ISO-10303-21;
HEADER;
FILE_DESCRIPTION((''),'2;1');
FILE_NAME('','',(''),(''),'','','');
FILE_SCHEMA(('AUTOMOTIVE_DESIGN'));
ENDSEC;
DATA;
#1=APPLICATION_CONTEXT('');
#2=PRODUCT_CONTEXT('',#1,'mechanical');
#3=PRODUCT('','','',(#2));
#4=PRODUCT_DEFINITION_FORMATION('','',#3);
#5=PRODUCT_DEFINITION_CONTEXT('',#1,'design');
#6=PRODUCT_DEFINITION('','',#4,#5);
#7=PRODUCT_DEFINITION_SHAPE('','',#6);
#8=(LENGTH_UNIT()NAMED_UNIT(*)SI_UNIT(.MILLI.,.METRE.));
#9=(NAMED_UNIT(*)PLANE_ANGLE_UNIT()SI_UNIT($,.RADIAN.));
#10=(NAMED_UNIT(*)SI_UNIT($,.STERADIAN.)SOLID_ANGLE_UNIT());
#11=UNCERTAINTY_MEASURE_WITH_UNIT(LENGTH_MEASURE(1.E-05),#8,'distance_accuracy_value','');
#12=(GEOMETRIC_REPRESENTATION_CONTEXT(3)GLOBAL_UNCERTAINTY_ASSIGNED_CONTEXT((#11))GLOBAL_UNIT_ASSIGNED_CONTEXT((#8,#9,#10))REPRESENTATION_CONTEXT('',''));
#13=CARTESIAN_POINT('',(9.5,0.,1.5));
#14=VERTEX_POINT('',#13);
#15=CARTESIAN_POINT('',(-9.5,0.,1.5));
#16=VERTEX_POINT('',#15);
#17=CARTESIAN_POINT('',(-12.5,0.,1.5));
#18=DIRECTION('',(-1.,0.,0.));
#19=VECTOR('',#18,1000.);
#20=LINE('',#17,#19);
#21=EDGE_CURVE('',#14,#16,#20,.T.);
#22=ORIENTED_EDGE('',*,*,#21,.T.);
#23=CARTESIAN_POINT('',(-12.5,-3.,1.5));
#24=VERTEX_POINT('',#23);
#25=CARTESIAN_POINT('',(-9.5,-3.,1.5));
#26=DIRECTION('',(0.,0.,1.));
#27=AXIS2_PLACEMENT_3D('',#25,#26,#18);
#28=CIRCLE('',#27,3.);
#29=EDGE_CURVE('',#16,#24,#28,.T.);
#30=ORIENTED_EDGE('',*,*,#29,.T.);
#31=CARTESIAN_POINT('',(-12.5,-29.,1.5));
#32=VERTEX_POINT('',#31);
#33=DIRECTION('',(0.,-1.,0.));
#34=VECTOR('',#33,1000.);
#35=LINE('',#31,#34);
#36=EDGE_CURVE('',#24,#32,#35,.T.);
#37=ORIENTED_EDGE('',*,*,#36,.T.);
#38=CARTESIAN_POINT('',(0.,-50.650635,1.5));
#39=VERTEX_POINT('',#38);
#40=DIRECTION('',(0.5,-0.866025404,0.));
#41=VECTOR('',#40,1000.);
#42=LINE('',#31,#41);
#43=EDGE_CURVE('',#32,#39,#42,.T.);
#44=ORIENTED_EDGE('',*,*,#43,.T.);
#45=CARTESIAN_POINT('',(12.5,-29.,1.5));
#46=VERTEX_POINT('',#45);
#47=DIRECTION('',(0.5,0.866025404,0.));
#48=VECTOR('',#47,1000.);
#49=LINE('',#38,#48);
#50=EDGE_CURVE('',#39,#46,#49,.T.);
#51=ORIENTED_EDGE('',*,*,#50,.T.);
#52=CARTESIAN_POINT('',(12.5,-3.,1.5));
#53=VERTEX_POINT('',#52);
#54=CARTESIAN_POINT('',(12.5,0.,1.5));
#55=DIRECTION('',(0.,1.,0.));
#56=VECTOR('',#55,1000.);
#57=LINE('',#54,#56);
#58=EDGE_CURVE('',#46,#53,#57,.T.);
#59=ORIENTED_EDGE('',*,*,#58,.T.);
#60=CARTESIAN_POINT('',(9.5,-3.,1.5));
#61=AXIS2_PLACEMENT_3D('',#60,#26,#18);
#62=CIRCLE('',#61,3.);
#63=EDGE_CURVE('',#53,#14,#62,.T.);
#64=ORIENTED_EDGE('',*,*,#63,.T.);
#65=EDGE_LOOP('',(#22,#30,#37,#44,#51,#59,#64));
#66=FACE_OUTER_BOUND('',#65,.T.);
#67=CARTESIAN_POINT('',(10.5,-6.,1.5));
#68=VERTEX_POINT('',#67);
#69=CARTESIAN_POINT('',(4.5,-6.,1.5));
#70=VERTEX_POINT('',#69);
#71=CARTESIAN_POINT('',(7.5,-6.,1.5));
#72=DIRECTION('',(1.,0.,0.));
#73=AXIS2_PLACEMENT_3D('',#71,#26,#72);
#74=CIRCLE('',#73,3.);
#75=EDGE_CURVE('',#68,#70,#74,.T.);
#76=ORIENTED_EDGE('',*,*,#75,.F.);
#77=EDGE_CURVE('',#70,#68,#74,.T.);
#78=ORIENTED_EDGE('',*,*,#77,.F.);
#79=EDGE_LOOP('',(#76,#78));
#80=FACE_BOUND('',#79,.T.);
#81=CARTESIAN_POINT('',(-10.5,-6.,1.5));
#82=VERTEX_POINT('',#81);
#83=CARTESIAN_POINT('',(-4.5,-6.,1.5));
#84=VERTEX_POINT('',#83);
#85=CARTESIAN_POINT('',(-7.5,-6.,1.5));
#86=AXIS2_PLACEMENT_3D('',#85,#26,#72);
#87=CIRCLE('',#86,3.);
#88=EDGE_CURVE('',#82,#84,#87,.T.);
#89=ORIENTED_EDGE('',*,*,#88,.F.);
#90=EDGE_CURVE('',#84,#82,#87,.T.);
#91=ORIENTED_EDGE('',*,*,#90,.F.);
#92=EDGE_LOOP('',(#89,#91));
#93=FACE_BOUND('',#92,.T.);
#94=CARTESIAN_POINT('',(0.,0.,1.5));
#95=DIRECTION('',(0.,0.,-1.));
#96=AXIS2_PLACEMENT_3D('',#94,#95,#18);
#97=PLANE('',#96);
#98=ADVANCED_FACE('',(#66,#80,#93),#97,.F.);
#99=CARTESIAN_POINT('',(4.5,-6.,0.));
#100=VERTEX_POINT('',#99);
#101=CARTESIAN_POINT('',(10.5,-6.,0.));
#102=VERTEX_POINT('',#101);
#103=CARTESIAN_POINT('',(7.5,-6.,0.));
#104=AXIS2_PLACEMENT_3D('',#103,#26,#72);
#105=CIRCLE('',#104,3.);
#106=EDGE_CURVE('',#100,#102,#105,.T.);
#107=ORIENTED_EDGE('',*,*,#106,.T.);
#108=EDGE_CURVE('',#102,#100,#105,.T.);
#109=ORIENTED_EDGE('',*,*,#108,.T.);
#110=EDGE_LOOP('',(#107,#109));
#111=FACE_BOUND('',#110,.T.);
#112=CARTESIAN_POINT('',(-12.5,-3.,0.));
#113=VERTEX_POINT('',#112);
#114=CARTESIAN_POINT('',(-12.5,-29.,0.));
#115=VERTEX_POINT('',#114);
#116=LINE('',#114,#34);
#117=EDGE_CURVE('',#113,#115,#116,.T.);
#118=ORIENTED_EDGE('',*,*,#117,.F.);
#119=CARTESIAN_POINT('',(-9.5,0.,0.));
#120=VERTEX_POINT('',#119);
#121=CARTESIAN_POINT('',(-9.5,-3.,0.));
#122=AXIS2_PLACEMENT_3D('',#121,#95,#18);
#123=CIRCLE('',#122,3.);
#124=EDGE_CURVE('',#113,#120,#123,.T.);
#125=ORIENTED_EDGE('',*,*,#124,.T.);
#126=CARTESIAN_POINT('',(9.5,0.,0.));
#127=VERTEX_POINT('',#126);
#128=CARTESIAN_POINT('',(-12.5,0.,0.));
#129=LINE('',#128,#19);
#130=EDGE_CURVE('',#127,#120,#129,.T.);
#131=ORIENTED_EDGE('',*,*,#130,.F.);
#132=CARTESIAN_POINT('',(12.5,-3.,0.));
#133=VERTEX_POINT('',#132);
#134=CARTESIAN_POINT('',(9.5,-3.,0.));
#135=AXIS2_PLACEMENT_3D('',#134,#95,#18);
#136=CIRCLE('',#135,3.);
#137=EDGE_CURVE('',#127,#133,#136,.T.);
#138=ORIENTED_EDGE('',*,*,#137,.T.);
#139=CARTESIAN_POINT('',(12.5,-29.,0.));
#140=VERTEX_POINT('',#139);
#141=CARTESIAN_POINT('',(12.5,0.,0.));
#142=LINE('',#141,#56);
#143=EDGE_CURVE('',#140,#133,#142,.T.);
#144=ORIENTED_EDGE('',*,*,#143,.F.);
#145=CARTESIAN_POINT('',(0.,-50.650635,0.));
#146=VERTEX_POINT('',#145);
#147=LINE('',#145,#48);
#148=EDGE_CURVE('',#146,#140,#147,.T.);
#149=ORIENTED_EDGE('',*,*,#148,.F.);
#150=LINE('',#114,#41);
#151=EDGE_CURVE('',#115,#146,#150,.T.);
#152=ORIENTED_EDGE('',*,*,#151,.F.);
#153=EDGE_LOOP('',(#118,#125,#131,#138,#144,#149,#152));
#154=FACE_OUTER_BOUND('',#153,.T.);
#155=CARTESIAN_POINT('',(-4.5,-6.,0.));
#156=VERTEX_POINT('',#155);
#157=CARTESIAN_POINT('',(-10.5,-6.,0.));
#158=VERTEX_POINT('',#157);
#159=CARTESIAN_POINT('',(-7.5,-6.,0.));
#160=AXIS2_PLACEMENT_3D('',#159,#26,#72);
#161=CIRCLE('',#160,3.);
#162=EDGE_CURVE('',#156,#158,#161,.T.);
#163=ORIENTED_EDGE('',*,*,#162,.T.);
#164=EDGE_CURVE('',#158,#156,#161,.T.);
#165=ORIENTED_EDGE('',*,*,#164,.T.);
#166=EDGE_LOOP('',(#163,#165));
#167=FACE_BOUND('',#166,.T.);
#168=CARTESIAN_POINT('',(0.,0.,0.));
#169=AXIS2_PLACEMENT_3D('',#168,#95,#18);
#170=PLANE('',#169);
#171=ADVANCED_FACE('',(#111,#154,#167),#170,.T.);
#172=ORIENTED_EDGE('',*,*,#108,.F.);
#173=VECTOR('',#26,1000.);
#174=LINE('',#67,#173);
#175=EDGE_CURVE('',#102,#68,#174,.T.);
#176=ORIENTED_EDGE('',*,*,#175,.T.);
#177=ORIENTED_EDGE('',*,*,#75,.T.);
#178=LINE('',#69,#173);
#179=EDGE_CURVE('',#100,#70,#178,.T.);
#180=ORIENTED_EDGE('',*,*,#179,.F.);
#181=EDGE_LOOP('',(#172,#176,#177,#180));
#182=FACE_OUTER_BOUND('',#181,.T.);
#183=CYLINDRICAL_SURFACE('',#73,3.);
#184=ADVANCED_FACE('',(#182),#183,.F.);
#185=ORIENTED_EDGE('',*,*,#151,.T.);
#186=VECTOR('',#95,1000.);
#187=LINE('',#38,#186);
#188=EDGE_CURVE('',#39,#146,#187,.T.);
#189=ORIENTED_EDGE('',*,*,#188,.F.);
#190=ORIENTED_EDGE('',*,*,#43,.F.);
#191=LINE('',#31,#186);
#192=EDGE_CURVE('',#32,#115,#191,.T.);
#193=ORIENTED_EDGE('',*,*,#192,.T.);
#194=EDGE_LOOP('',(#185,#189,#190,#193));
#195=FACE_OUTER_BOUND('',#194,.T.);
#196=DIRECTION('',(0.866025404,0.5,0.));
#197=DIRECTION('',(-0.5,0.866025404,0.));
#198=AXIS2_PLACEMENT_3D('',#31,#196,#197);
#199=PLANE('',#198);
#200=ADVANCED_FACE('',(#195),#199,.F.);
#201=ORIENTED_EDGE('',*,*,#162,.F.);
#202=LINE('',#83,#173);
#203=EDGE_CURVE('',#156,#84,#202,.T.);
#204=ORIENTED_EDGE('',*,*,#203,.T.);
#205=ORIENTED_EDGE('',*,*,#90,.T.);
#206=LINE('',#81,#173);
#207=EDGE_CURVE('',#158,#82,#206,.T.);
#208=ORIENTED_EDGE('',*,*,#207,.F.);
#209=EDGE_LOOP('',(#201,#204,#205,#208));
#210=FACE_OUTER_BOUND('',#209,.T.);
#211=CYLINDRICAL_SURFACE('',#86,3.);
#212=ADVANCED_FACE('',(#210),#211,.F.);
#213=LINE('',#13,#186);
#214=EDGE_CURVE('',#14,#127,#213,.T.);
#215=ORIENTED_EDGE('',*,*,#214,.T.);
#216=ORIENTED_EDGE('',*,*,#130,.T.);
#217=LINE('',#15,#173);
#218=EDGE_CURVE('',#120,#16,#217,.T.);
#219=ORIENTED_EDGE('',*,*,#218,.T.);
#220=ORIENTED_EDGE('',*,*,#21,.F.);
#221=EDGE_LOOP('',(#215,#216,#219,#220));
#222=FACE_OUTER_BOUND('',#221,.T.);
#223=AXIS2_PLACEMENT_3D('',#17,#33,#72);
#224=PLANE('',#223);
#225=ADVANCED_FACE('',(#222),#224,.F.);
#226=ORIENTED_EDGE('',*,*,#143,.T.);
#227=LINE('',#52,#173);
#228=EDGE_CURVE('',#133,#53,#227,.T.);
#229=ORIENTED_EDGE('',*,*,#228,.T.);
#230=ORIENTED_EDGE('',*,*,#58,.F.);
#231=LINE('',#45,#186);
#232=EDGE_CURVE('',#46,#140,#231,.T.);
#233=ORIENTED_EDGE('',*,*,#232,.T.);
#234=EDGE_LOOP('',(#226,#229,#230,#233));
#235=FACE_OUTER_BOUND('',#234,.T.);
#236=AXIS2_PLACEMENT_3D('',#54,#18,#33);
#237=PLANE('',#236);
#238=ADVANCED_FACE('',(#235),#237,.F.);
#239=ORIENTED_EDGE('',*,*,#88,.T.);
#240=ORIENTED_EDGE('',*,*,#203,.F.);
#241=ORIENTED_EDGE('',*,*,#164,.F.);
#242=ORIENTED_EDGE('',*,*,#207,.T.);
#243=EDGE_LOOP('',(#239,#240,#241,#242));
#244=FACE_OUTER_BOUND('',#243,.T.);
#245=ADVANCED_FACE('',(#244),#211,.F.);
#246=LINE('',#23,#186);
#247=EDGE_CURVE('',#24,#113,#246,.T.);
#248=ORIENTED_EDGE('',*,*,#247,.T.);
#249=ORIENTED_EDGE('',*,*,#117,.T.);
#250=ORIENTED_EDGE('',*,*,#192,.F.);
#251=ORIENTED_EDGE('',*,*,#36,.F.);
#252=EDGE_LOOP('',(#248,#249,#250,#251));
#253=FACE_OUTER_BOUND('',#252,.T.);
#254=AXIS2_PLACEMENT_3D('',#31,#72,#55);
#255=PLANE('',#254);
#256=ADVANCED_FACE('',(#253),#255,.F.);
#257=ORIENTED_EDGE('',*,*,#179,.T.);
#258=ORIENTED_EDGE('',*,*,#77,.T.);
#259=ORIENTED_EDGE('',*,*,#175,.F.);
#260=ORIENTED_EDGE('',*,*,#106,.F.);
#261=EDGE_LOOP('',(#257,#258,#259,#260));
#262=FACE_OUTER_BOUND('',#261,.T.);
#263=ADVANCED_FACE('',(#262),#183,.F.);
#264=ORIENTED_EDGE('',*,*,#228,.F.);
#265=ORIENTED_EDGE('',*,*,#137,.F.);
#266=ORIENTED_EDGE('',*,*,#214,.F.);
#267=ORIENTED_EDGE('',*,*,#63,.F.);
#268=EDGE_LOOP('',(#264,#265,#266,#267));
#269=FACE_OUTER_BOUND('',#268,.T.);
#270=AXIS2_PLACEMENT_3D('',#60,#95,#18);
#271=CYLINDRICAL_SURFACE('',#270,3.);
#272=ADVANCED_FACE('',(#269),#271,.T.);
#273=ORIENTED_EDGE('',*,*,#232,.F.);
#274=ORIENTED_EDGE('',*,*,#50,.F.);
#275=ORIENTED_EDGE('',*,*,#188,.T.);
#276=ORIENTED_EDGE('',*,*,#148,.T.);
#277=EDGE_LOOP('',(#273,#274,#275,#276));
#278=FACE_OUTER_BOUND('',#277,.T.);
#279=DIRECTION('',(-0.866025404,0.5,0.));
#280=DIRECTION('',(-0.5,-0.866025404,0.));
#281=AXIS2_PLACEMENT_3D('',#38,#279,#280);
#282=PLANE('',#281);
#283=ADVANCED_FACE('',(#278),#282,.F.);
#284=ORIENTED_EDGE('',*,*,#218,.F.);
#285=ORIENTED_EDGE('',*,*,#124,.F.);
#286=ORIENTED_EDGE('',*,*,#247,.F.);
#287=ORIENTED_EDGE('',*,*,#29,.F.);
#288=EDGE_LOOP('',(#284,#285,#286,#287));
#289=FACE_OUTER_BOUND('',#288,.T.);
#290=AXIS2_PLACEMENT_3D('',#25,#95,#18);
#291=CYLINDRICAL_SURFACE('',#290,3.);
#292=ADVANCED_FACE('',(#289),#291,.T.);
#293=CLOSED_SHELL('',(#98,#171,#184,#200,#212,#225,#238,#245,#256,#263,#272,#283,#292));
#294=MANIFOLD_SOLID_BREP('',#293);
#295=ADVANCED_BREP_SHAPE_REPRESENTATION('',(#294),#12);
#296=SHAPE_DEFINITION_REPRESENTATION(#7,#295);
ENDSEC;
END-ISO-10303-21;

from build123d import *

# Parameters (mm, degrees)
EXTRUDE_1_DEPTH       = 1.5
HOLE_WIZARD_6_0_6_1_D = 6
FILLET_1_R            = 3


with BuildPart() as part:
    # 草图1 → 凸台-拉伸1 (new body)
    with BuildSketch(Plane.XY):
        Polygon((-12.5, 0), (12.5, 0), (12.5, -29), (0, -50.650635095), (-12.5, -29), align=None)
    extrude(amount=EXTRUDE_1_DEPTH)

    # Ø6.0 (6) 直径孔1 (through all)
    with Locations(Plane.XY.offset(1.5)):
        with Locations((-7.5, -6), (7.5, -6)):
            Hole(HOLE_WIZARD_6_0_6_1_D / 2)

    # 圆角1
    fillet_1_edges = [part.edges().sort_by_distance(p)[0] for p in [
        (-12.5, 0, 0.75),
        (12.5, 0, 0.75),
    ]]
    fillet(fillet_1_edges, radius=FILLET_1_R)


solid = part.part
